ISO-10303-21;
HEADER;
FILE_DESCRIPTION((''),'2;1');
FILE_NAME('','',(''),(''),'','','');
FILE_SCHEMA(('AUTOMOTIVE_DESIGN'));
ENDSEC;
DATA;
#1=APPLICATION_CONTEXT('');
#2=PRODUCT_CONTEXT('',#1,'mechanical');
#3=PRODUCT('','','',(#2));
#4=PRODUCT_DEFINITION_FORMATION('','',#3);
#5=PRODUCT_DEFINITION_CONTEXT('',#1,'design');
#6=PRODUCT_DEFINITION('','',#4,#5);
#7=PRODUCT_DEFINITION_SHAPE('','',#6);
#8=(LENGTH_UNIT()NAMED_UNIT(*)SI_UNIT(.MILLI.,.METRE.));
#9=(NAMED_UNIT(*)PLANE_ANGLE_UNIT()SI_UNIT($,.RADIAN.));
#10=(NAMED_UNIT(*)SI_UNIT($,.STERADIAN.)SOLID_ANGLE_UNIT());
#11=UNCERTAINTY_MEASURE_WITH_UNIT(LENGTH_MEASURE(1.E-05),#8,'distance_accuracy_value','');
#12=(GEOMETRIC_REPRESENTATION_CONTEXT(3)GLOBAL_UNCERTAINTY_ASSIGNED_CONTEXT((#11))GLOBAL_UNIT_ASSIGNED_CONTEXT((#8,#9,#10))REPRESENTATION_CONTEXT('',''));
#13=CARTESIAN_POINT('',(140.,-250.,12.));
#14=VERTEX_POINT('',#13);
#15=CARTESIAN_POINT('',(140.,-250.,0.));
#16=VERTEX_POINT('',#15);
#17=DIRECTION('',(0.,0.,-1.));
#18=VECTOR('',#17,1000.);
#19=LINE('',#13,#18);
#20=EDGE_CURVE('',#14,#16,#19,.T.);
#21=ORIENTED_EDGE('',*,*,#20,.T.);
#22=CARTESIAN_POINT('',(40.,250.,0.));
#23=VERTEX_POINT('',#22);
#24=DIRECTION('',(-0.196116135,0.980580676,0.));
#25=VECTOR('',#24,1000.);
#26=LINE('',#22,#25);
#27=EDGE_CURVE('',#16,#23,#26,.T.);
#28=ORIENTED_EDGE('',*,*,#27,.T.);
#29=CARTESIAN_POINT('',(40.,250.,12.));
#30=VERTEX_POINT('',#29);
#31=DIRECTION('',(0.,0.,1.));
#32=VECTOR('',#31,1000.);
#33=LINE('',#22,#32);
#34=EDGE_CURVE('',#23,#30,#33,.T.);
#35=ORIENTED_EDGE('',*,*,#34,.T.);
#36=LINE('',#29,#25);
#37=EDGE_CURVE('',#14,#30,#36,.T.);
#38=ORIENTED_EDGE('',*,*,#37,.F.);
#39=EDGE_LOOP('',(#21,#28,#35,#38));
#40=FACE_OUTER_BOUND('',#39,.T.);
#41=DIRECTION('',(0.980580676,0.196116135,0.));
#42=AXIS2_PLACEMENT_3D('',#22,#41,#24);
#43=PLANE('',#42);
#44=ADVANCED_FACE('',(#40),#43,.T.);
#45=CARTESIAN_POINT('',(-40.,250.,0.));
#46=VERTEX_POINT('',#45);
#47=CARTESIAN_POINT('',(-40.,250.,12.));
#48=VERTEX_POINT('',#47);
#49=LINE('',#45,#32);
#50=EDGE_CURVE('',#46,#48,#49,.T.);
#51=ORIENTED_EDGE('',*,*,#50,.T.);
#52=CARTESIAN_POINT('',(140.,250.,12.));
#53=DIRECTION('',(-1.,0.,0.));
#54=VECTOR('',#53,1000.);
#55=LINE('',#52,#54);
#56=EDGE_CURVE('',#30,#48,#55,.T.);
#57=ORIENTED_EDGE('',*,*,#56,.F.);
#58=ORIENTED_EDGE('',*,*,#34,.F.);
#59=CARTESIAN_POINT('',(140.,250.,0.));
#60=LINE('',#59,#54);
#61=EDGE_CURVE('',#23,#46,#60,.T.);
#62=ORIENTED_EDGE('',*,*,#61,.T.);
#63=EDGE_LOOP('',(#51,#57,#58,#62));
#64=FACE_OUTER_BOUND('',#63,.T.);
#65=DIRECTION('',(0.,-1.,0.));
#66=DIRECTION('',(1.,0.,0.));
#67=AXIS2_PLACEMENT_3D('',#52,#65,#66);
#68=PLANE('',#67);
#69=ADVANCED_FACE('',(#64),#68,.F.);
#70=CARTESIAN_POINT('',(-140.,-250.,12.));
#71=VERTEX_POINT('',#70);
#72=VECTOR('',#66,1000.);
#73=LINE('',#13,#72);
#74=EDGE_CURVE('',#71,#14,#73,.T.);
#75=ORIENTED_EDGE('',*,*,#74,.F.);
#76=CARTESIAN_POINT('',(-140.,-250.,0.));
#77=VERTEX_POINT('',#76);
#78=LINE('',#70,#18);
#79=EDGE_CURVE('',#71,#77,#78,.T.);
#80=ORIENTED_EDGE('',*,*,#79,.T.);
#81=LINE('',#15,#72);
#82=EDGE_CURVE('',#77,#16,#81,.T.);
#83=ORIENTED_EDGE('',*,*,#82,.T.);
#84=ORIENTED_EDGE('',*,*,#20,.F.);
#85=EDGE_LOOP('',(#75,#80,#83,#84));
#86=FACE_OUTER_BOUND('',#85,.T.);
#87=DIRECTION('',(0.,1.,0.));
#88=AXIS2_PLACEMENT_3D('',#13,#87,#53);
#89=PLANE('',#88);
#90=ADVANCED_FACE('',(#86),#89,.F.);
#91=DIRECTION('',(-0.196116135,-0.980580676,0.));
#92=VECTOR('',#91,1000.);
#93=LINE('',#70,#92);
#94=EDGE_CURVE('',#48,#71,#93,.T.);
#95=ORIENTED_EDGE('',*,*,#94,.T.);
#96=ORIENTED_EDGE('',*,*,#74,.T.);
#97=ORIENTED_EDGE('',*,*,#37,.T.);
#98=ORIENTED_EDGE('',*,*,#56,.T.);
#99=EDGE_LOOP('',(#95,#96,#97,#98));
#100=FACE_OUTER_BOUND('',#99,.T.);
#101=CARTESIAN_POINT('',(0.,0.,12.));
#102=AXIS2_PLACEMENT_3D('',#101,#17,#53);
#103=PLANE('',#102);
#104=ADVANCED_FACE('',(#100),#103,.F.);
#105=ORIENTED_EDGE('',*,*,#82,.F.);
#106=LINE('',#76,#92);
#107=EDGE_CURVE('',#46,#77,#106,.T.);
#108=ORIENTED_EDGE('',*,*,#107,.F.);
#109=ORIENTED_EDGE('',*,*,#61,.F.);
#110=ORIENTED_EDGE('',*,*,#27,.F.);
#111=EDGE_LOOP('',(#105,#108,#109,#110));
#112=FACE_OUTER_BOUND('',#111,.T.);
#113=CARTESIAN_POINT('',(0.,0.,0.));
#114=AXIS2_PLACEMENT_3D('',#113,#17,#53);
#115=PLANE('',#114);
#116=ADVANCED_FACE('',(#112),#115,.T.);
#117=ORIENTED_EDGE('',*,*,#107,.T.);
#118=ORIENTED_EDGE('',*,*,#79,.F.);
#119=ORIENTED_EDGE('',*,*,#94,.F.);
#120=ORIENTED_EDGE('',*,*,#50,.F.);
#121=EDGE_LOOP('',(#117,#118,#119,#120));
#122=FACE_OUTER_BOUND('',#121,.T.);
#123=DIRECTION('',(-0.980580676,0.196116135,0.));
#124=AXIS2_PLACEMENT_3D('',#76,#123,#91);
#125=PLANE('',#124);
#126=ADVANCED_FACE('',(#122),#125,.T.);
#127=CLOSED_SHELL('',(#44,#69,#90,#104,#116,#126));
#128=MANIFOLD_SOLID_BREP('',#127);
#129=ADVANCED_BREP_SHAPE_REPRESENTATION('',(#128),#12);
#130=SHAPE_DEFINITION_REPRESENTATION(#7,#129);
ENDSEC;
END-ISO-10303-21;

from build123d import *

# Parameters (mm, degrees)
SKETCH_1_W          = 280
SKETCH_1_H          = 500
EXTRUDE_1_DEPTH     = 12
SKETCH_2_OUTSIDE_W  = 396.638
SKETCH_2_OUTSIDE_H  = 616.638
CUT_EXTRUDE_1_DEPTH = 12


with BuildPart() as part:
    # 草图1 → 凸台-拉伸1 (new body)
    with BuildSketch(Plane.XY):
        Rectangle(SKETCH_1_W, SKETCH_1_H)
    extrude(amount=EXTRUDE_1_DEPTH)

    # 草图2 outside → 切除-拉伸1 (cut)
    with BuildSketch(Plane.XY.offset(12)):
        Rectangle(SKETCH_2_OUTSIDE_W, SKETCH_2_OUTSIDE_H)
        Polygon((-140, -250), (-40, 250), (40, 250), (140, -250), align=None, mode=Mode.SUBTRACT)
    extrude(amount=-CUT_EXTRUDE_1_DEPTH, mode=Mode.SUBTRACT)


solid = part.part
